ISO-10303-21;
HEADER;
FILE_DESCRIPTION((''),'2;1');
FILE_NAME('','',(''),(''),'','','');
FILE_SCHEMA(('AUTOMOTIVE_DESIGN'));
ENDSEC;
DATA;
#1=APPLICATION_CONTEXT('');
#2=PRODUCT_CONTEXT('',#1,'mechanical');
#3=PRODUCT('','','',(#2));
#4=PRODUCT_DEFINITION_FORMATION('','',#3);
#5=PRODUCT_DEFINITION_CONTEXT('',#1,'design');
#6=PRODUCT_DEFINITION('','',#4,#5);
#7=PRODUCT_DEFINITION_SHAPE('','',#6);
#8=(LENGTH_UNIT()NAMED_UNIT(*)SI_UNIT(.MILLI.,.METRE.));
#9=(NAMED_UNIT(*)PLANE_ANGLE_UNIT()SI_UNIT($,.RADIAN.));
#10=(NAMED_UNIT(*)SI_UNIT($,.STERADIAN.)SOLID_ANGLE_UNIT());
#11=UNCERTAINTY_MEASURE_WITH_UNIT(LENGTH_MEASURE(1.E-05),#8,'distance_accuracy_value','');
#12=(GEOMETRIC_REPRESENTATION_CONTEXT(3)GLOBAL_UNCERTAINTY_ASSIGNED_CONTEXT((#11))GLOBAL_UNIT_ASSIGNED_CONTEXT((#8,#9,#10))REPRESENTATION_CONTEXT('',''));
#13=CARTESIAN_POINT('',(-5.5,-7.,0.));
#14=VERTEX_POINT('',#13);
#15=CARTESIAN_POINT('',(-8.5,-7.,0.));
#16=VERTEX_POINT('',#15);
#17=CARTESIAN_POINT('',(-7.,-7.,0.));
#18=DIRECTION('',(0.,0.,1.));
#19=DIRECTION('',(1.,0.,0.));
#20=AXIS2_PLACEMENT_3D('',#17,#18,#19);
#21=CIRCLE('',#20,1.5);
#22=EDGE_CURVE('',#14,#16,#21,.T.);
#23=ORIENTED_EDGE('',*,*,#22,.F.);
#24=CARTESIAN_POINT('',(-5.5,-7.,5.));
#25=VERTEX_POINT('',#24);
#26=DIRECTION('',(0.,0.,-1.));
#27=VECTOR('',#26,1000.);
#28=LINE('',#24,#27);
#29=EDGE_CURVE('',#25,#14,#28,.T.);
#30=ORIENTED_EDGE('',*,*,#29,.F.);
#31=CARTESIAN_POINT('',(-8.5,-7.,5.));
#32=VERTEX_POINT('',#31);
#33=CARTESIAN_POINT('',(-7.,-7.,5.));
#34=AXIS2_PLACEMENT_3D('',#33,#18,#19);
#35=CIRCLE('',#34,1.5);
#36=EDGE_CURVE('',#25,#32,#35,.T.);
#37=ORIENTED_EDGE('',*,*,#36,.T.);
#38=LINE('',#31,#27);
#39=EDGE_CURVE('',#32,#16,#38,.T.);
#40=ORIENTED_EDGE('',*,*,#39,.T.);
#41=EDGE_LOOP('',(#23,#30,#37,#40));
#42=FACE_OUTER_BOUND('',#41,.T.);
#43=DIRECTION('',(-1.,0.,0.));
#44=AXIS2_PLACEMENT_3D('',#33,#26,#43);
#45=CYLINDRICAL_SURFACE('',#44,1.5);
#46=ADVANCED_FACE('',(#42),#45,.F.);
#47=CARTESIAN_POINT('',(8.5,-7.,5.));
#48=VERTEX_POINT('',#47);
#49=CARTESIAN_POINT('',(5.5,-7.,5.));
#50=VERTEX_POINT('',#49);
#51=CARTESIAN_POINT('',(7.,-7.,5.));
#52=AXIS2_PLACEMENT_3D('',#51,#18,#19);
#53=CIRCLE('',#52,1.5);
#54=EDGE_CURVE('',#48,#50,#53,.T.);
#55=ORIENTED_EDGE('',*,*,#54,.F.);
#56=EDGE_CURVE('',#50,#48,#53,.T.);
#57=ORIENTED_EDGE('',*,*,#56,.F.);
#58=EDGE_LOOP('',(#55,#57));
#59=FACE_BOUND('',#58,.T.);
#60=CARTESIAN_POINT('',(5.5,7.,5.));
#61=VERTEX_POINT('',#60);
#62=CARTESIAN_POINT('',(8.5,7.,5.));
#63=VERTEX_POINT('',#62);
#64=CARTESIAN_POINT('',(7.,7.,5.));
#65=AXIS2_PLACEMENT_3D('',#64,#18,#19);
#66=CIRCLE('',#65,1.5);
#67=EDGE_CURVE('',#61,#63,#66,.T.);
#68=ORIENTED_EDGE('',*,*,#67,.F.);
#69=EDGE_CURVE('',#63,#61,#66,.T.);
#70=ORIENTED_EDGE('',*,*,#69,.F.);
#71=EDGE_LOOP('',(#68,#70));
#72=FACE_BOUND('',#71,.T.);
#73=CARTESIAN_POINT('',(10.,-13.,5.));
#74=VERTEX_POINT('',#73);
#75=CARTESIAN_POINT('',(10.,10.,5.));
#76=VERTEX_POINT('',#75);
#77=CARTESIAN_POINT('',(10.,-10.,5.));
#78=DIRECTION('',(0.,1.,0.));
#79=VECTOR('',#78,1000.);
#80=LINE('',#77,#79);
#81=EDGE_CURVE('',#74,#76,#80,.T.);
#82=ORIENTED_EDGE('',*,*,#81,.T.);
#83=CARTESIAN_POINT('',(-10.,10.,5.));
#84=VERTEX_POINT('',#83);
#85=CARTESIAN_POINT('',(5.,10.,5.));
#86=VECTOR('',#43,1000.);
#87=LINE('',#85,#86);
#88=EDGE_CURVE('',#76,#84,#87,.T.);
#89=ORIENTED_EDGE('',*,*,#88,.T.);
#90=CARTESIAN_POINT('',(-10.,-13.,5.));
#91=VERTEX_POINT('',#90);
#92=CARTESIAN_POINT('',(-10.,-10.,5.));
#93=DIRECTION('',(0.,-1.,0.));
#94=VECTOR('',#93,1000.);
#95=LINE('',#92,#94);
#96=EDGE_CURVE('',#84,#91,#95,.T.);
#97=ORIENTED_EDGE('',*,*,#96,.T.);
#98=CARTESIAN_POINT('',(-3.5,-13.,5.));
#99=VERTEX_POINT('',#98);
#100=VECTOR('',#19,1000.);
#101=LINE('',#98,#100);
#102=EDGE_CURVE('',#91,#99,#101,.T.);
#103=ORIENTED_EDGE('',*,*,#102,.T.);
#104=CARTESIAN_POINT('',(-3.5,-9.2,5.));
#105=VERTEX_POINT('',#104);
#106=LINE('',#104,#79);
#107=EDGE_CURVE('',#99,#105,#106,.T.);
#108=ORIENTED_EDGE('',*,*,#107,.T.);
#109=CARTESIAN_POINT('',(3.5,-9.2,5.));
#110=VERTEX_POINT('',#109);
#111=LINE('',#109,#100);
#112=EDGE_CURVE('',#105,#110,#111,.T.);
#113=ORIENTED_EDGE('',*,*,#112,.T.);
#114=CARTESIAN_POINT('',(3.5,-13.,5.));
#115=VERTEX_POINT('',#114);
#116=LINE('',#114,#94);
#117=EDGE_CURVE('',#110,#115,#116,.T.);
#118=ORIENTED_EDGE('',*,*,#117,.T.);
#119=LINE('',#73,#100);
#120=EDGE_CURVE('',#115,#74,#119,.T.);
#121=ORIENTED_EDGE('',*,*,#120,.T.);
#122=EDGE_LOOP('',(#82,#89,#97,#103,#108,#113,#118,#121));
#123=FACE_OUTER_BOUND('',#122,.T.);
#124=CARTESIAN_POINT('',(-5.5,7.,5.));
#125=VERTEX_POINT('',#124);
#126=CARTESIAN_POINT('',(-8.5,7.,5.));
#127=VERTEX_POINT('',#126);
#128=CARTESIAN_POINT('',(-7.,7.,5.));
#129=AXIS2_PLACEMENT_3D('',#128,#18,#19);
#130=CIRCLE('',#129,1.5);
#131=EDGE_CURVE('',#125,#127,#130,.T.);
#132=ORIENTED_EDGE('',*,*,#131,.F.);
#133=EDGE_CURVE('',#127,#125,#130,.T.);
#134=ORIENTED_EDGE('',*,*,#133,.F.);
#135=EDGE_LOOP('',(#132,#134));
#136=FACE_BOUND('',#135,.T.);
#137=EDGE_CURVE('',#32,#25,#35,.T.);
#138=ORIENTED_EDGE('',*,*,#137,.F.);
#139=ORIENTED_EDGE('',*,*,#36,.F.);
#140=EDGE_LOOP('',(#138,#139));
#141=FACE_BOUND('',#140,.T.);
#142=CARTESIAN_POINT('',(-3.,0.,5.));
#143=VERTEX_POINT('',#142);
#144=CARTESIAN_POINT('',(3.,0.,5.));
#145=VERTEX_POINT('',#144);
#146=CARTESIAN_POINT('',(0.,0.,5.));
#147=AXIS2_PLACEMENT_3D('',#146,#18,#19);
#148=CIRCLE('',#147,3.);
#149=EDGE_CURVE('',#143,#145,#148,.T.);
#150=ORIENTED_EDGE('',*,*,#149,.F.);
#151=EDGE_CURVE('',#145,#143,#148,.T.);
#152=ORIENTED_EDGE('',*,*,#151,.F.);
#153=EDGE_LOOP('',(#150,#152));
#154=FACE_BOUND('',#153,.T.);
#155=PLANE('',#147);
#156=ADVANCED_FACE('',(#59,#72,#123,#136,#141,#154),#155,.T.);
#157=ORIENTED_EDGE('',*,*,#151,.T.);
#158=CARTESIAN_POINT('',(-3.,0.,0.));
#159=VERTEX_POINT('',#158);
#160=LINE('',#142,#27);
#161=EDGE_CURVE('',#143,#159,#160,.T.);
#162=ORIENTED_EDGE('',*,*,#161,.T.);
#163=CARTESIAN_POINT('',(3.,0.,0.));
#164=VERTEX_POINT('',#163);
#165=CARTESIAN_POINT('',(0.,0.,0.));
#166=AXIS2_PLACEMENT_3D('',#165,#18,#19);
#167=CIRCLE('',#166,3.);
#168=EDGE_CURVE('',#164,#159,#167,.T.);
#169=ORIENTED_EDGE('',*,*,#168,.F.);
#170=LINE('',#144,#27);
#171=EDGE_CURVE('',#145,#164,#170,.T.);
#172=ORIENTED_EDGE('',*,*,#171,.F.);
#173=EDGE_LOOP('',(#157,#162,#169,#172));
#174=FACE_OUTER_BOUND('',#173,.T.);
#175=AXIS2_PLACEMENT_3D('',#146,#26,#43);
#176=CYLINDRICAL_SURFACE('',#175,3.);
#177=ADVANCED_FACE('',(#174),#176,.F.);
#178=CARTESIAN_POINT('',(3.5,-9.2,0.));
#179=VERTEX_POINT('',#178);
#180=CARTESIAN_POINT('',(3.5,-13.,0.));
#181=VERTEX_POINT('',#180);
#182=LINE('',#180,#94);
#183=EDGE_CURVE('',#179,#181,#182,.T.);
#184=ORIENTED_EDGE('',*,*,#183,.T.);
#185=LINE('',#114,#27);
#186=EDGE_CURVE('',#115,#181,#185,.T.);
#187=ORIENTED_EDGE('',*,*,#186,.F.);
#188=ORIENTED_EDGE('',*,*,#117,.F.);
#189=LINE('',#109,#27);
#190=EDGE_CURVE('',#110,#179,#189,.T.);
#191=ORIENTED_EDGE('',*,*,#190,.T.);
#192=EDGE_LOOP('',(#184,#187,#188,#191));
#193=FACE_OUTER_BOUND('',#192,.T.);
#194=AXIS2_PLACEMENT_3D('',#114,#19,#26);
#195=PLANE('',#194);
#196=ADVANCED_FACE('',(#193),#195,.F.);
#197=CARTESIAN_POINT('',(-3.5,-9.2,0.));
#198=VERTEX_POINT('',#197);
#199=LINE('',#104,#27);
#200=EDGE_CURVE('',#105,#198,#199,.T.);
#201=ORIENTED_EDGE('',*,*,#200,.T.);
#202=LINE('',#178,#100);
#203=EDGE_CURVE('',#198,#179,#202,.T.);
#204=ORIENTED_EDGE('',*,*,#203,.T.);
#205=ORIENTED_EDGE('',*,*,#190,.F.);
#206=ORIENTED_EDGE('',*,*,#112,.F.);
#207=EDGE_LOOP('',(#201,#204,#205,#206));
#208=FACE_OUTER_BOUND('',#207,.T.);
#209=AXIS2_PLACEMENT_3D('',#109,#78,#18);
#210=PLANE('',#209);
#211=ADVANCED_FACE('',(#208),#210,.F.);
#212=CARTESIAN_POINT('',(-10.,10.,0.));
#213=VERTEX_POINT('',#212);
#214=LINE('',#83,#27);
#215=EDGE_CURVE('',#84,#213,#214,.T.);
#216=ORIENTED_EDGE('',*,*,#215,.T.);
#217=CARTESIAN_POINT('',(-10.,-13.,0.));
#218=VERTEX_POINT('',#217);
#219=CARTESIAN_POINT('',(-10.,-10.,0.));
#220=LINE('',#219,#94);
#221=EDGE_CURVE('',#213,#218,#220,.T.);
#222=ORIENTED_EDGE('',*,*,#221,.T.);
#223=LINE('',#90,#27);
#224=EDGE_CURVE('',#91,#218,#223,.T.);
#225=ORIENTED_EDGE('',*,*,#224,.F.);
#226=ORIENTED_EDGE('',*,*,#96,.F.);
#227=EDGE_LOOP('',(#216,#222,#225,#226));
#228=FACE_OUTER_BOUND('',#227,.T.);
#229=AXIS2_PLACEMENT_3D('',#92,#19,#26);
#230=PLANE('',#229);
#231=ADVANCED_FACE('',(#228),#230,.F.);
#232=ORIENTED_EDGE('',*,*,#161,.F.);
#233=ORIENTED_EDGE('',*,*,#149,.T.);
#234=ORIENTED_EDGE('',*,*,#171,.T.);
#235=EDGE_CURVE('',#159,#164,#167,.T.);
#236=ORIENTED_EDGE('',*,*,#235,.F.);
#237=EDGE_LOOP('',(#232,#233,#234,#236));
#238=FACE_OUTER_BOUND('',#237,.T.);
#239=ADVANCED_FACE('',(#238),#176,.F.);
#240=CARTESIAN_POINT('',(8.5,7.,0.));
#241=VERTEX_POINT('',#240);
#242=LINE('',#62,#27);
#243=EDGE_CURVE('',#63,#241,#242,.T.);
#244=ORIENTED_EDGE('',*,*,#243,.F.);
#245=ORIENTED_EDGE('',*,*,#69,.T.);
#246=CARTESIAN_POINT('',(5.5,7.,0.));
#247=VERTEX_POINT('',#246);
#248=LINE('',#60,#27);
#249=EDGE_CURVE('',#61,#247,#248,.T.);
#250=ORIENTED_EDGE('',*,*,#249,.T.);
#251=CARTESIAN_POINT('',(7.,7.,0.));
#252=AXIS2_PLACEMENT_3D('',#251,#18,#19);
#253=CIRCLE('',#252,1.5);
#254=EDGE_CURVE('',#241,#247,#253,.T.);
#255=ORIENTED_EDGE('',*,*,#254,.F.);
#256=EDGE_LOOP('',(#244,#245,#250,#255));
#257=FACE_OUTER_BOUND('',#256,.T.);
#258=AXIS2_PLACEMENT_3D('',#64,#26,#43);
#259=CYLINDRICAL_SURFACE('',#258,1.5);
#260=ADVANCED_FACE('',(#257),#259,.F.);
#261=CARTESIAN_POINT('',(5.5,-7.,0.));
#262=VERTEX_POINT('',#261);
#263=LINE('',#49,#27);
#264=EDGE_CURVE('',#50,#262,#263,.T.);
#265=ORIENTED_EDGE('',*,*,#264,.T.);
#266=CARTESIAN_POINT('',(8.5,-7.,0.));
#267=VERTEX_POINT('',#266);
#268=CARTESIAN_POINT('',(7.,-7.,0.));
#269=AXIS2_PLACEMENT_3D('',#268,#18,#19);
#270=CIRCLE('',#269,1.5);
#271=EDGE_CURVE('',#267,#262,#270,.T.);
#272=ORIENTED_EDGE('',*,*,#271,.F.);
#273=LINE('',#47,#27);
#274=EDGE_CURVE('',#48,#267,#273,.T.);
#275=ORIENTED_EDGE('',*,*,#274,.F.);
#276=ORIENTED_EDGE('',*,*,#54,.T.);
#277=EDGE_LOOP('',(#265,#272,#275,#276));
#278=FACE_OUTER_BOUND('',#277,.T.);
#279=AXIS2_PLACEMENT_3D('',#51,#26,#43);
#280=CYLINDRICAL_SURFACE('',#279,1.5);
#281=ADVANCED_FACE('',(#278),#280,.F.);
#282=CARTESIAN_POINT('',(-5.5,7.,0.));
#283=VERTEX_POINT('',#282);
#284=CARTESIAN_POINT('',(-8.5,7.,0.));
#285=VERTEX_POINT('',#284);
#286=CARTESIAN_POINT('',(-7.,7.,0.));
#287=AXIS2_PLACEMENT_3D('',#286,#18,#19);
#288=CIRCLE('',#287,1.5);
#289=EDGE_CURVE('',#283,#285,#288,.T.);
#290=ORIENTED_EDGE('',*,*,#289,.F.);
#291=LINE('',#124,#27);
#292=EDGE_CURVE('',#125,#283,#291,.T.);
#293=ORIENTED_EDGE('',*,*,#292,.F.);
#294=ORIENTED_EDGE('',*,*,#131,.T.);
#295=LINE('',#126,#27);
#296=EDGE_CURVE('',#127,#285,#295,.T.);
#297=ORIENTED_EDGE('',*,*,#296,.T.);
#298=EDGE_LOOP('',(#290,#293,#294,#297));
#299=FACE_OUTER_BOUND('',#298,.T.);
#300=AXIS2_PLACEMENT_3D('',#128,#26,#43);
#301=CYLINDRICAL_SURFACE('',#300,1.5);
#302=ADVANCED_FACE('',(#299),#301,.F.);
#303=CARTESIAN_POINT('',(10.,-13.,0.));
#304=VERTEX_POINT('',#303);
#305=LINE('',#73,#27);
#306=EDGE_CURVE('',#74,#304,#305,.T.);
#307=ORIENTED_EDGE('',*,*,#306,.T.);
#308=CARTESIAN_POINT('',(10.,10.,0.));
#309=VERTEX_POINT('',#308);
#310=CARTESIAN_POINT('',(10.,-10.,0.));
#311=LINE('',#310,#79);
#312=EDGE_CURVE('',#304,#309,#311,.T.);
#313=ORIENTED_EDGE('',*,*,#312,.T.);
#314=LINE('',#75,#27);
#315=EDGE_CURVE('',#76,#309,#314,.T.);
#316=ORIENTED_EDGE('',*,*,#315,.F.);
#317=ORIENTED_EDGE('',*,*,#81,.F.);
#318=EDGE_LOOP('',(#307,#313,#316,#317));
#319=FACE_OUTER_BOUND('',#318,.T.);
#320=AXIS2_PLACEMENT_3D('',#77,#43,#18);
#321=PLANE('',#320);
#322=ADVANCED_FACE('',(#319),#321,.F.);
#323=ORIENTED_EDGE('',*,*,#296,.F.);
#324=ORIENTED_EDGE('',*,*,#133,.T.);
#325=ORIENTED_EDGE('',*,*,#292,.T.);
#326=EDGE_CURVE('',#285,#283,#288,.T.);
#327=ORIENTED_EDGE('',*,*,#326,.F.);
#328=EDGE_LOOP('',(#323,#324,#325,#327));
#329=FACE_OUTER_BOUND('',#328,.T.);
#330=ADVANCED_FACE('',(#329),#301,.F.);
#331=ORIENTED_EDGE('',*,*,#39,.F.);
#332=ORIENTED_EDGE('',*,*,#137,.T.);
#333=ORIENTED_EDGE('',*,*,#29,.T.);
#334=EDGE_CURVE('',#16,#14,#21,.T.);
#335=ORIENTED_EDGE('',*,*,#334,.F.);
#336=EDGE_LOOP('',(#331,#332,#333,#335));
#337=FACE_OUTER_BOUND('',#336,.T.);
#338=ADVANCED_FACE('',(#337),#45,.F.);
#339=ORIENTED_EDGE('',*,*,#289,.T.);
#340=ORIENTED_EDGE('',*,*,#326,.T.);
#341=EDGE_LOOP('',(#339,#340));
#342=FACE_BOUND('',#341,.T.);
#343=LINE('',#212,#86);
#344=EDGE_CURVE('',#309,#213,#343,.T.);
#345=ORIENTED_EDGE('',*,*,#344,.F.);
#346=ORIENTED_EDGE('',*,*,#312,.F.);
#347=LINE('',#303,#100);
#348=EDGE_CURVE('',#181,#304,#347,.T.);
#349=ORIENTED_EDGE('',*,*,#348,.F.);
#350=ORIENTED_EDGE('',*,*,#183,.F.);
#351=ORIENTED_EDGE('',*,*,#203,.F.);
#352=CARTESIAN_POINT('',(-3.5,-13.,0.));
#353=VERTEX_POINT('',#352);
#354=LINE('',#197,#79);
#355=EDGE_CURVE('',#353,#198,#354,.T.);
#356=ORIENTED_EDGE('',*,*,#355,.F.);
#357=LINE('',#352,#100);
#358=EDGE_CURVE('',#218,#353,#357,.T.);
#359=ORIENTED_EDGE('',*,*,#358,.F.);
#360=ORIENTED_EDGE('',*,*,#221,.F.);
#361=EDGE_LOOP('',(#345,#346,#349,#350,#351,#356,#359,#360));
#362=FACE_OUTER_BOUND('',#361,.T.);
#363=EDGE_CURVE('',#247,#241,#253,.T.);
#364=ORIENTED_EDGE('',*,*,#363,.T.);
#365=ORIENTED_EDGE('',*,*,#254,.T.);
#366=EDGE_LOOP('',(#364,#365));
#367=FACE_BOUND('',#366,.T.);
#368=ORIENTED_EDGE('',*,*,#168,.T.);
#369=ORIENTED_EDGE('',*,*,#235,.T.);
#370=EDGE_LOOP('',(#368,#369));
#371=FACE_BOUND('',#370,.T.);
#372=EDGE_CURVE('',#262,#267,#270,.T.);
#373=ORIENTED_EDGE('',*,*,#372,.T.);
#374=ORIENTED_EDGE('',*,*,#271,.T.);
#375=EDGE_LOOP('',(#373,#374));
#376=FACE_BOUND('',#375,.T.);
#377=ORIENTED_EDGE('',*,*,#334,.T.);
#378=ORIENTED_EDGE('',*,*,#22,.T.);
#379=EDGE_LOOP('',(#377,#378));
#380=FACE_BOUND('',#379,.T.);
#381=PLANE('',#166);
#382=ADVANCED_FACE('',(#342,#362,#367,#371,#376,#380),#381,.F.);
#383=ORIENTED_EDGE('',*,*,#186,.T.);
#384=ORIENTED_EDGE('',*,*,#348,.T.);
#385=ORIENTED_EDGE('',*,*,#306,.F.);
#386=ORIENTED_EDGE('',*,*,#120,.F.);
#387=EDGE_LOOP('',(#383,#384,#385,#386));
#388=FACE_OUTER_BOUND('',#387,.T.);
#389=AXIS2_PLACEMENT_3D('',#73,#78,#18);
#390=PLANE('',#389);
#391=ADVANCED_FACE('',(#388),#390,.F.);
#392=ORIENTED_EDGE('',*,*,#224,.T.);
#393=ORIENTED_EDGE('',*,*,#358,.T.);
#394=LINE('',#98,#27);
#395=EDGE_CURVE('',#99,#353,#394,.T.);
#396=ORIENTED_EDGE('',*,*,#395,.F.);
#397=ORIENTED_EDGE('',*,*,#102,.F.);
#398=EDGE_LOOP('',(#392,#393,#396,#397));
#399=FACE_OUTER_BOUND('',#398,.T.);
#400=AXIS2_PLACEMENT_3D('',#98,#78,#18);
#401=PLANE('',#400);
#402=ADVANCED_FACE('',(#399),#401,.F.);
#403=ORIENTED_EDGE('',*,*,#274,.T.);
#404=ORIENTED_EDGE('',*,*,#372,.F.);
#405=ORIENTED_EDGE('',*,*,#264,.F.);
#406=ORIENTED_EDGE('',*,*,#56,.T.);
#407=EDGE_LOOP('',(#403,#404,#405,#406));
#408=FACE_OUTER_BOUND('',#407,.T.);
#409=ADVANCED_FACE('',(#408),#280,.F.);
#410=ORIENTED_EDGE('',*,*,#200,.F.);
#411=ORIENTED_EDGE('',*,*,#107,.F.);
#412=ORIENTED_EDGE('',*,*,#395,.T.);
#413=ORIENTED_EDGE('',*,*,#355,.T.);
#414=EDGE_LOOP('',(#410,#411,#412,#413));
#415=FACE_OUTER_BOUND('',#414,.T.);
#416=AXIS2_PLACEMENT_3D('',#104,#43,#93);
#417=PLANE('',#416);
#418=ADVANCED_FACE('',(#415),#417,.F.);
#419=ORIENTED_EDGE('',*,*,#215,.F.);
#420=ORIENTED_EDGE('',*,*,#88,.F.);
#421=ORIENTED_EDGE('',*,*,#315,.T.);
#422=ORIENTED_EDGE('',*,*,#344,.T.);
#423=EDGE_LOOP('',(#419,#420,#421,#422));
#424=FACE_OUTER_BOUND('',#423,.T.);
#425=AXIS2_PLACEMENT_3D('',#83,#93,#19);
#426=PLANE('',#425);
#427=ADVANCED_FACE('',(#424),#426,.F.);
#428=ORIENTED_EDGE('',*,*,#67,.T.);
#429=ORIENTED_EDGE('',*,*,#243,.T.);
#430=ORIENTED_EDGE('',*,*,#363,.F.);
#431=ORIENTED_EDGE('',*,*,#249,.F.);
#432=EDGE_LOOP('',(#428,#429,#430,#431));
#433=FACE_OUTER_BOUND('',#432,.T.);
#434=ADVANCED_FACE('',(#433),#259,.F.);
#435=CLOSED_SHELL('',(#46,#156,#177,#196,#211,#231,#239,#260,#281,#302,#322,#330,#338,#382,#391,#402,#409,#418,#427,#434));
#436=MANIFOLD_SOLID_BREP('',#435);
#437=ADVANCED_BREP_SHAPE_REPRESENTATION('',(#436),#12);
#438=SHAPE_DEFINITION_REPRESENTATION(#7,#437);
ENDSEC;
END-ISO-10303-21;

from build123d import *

# Parameters (mm, degrees)
SKETCH1_R           = 3
SKETCH1_R_2         = 1.5
BOSS_EXTRUDE1_DEPTH = 5


with BuildPart() as part:
    # Sketch1 → Boss-Extrude1 (new body)
    with BuildSketch(Plane.XY):
        Polygon((-10, -10), (-10, 10), (-5, 10), (5, 10), (10, 10), (10, -10), (10, -13), (3.5, -13), (3.5, -9.2), (-3.5, -9.2), (-3.5, -13), (-10, -13), align=None)
        Circle(SKETCH1_R, mode=Mode.SUBTRACT)
        with Locations((-7, 7)):
            Circle(SKETCH1_R_2, mode=Mode.SUBTRACT)
        with Locations((7, 7)):
            Circle(SKETCH1_R_2, mode=Mode.SUBTRACT)
        with Locations((7, -7)):
            Circle(SKETCH1_R_2, mode=Mode.SUBTRACT)
        with Locations((-7, -7)):
            Circle(SKETCH1_R_2, mode=Mode.SUBTRACT)
    extrude(amount=BOSS_EXTRUDE1_DEPTH)


solid = part.part
